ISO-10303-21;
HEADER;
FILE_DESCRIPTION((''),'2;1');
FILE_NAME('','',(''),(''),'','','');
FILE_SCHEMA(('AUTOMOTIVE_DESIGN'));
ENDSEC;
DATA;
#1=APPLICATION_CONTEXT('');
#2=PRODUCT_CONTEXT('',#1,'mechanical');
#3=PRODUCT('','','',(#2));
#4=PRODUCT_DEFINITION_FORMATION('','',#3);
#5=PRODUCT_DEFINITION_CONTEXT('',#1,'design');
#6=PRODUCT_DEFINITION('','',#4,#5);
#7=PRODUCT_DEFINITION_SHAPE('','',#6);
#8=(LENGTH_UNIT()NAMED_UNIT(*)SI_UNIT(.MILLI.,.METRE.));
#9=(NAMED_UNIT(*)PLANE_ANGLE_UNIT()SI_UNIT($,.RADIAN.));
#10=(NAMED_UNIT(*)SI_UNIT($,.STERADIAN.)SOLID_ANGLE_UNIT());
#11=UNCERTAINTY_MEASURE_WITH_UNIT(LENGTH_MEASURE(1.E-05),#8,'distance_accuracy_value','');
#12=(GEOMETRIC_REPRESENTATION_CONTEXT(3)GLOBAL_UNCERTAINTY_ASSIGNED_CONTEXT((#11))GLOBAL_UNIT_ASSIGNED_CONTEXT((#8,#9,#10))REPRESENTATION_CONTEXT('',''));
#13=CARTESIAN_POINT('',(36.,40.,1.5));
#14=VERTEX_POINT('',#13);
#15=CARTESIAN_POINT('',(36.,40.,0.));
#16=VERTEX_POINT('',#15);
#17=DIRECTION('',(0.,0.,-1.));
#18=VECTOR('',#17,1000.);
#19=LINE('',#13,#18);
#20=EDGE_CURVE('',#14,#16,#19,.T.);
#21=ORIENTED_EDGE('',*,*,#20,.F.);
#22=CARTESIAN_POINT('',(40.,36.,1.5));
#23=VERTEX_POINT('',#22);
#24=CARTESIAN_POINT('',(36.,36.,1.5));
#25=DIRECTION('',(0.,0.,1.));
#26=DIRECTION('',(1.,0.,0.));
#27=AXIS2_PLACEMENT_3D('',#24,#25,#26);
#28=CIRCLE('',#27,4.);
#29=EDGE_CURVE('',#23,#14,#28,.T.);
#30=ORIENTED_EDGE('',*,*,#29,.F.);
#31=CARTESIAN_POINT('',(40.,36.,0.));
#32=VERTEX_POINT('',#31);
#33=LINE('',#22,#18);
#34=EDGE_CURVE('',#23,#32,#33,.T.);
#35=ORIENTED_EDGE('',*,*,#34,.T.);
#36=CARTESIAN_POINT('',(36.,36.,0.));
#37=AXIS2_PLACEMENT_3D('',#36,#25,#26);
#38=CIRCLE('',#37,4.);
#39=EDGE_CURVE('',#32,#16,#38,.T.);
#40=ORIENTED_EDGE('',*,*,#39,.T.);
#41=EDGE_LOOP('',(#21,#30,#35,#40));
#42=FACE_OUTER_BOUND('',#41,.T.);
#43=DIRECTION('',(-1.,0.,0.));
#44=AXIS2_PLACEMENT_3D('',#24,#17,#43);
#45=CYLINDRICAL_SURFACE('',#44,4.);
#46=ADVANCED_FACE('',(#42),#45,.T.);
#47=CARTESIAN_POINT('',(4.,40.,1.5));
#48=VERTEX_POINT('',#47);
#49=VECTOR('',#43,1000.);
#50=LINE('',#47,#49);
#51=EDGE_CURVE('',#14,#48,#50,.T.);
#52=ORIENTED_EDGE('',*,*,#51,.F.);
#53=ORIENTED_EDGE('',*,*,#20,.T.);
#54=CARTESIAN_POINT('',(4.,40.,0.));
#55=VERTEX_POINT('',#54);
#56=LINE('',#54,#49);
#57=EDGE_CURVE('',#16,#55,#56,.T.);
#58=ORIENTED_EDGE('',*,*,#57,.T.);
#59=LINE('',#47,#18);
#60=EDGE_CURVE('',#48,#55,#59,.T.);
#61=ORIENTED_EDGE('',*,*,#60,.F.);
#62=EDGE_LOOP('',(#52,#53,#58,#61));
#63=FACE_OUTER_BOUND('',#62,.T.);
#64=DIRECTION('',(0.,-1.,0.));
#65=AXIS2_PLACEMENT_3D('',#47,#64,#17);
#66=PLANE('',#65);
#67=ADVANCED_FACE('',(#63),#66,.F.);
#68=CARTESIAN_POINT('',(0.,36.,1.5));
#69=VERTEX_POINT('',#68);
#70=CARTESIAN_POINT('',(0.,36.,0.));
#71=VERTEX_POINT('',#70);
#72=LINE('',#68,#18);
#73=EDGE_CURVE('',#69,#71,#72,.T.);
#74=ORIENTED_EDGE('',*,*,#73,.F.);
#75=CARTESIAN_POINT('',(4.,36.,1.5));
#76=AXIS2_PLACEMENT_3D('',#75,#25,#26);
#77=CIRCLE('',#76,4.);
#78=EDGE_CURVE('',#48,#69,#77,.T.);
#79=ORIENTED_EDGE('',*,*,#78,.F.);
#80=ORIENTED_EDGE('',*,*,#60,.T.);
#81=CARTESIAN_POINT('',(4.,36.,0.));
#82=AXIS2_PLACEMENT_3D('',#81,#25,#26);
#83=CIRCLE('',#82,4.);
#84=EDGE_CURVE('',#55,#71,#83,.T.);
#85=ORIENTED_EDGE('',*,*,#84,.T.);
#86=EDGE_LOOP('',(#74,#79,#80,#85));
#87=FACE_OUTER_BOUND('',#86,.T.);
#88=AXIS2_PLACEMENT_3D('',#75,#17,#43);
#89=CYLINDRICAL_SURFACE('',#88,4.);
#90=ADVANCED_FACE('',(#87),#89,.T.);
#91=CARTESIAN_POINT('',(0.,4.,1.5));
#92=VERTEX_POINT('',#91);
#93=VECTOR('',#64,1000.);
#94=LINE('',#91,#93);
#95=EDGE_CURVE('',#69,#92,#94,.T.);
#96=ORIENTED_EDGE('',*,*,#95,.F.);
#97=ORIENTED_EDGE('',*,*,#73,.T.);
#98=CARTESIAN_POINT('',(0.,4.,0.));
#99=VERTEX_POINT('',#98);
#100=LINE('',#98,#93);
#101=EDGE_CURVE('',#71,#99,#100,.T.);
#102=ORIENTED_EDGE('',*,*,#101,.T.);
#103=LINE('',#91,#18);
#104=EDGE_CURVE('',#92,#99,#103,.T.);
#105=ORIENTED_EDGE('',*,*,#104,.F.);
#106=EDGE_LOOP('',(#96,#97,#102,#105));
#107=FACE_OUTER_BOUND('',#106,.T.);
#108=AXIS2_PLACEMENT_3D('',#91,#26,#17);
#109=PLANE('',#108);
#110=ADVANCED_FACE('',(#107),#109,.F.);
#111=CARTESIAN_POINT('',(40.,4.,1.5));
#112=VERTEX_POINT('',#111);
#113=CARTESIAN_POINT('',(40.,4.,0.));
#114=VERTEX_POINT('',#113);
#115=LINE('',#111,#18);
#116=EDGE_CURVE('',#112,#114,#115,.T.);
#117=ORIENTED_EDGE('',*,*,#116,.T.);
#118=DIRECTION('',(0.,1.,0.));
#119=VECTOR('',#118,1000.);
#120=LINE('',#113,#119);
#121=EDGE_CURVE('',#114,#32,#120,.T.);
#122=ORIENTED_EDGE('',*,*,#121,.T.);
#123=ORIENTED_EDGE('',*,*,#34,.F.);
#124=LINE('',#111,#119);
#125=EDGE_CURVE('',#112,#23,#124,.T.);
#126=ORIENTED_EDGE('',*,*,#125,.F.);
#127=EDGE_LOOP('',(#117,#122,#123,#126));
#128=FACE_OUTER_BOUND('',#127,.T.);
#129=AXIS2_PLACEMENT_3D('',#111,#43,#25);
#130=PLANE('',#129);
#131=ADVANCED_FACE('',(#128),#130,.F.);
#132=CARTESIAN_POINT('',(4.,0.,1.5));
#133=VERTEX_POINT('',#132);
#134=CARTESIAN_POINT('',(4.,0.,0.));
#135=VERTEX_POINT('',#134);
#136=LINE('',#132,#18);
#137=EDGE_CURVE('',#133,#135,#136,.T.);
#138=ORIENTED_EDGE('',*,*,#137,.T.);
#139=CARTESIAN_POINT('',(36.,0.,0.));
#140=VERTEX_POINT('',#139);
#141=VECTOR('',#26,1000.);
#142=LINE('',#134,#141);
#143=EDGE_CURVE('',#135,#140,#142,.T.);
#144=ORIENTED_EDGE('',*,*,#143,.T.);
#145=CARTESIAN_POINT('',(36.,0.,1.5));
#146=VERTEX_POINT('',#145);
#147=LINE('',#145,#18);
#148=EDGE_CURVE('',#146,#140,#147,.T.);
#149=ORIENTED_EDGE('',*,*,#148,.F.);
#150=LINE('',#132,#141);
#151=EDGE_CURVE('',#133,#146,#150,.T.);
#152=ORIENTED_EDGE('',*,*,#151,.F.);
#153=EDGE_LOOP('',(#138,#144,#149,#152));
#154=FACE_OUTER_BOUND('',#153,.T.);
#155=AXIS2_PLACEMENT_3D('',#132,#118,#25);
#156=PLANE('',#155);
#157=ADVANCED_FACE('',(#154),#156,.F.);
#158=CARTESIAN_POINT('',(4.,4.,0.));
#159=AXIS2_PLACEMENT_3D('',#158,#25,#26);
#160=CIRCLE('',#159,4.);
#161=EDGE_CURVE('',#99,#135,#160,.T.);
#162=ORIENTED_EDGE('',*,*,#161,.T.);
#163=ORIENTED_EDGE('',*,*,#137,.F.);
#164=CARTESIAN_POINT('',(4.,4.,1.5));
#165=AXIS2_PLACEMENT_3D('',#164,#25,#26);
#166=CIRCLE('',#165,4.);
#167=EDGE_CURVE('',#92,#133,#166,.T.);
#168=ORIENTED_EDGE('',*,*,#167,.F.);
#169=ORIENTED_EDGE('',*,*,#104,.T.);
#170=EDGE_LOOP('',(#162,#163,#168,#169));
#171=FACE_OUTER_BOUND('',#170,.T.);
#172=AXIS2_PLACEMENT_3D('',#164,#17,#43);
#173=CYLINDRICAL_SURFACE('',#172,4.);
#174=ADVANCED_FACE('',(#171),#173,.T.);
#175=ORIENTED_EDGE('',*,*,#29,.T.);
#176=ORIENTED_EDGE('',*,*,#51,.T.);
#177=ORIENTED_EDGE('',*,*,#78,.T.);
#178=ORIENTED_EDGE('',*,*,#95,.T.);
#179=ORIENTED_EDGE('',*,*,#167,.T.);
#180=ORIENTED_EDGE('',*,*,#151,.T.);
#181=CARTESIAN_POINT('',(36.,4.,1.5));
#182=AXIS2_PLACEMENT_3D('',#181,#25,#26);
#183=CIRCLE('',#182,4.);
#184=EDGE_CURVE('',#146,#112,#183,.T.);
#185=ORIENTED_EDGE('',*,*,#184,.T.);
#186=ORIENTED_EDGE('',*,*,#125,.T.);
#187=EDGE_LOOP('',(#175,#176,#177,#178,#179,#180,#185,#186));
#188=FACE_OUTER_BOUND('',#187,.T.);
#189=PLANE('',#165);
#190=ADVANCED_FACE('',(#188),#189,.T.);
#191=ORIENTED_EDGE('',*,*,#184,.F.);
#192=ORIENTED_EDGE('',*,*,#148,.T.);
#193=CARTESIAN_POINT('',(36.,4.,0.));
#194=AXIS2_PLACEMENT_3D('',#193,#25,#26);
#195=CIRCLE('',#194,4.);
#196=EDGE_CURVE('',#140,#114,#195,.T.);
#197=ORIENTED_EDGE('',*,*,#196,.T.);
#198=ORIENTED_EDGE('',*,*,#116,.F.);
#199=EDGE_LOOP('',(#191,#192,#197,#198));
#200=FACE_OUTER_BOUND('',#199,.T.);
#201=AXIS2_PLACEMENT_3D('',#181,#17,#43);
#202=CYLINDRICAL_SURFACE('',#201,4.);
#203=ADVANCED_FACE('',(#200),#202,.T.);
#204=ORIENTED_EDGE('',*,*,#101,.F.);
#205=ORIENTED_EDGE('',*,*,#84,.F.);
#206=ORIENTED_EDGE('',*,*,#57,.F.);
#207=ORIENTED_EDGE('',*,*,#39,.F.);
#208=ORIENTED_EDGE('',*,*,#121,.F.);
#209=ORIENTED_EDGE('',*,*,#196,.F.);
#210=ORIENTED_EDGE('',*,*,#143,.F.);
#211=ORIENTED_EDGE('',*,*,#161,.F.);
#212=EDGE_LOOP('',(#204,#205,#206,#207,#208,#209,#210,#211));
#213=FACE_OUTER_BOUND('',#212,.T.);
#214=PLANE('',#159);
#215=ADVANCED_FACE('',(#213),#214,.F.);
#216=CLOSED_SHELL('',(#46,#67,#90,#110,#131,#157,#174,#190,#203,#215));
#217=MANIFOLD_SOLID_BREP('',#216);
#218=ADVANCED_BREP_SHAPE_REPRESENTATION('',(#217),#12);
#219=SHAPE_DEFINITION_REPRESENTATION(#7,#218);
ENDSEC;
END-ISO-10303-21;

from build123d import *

# Parameters (mm, degrees)
BOSS_EXTRUDE1_DEPTH = 1.5


with BuildPart() as part:
    # Sketch1 → Boss-Extrude1 (new body)
    with BuildSketch(Plane.XY):
        with BuildLine():
            Line((4, 0), (36, 0))
            ThreePointArc((36, 0), (38.828427125, 1.171572875), (40, 4))
            Line((40, 4), (40, 36))
            ThreePointArc((40, 36), (38.828427125, 38.828427125), (36, 40))
            Line((36, 40), (4, 40))
            ThreePointArc((4, 40), (1.171572875, 38.828427125), (0, 36))
            Line((0, 36), (0, 4))
            ThreePointArc((0, 4), (1.171572875, 1.171572875), (4, 0))
        make_face()
    extrude(amount=BOSS_EXTRUDE1_DEPTH)


solid = part.part
